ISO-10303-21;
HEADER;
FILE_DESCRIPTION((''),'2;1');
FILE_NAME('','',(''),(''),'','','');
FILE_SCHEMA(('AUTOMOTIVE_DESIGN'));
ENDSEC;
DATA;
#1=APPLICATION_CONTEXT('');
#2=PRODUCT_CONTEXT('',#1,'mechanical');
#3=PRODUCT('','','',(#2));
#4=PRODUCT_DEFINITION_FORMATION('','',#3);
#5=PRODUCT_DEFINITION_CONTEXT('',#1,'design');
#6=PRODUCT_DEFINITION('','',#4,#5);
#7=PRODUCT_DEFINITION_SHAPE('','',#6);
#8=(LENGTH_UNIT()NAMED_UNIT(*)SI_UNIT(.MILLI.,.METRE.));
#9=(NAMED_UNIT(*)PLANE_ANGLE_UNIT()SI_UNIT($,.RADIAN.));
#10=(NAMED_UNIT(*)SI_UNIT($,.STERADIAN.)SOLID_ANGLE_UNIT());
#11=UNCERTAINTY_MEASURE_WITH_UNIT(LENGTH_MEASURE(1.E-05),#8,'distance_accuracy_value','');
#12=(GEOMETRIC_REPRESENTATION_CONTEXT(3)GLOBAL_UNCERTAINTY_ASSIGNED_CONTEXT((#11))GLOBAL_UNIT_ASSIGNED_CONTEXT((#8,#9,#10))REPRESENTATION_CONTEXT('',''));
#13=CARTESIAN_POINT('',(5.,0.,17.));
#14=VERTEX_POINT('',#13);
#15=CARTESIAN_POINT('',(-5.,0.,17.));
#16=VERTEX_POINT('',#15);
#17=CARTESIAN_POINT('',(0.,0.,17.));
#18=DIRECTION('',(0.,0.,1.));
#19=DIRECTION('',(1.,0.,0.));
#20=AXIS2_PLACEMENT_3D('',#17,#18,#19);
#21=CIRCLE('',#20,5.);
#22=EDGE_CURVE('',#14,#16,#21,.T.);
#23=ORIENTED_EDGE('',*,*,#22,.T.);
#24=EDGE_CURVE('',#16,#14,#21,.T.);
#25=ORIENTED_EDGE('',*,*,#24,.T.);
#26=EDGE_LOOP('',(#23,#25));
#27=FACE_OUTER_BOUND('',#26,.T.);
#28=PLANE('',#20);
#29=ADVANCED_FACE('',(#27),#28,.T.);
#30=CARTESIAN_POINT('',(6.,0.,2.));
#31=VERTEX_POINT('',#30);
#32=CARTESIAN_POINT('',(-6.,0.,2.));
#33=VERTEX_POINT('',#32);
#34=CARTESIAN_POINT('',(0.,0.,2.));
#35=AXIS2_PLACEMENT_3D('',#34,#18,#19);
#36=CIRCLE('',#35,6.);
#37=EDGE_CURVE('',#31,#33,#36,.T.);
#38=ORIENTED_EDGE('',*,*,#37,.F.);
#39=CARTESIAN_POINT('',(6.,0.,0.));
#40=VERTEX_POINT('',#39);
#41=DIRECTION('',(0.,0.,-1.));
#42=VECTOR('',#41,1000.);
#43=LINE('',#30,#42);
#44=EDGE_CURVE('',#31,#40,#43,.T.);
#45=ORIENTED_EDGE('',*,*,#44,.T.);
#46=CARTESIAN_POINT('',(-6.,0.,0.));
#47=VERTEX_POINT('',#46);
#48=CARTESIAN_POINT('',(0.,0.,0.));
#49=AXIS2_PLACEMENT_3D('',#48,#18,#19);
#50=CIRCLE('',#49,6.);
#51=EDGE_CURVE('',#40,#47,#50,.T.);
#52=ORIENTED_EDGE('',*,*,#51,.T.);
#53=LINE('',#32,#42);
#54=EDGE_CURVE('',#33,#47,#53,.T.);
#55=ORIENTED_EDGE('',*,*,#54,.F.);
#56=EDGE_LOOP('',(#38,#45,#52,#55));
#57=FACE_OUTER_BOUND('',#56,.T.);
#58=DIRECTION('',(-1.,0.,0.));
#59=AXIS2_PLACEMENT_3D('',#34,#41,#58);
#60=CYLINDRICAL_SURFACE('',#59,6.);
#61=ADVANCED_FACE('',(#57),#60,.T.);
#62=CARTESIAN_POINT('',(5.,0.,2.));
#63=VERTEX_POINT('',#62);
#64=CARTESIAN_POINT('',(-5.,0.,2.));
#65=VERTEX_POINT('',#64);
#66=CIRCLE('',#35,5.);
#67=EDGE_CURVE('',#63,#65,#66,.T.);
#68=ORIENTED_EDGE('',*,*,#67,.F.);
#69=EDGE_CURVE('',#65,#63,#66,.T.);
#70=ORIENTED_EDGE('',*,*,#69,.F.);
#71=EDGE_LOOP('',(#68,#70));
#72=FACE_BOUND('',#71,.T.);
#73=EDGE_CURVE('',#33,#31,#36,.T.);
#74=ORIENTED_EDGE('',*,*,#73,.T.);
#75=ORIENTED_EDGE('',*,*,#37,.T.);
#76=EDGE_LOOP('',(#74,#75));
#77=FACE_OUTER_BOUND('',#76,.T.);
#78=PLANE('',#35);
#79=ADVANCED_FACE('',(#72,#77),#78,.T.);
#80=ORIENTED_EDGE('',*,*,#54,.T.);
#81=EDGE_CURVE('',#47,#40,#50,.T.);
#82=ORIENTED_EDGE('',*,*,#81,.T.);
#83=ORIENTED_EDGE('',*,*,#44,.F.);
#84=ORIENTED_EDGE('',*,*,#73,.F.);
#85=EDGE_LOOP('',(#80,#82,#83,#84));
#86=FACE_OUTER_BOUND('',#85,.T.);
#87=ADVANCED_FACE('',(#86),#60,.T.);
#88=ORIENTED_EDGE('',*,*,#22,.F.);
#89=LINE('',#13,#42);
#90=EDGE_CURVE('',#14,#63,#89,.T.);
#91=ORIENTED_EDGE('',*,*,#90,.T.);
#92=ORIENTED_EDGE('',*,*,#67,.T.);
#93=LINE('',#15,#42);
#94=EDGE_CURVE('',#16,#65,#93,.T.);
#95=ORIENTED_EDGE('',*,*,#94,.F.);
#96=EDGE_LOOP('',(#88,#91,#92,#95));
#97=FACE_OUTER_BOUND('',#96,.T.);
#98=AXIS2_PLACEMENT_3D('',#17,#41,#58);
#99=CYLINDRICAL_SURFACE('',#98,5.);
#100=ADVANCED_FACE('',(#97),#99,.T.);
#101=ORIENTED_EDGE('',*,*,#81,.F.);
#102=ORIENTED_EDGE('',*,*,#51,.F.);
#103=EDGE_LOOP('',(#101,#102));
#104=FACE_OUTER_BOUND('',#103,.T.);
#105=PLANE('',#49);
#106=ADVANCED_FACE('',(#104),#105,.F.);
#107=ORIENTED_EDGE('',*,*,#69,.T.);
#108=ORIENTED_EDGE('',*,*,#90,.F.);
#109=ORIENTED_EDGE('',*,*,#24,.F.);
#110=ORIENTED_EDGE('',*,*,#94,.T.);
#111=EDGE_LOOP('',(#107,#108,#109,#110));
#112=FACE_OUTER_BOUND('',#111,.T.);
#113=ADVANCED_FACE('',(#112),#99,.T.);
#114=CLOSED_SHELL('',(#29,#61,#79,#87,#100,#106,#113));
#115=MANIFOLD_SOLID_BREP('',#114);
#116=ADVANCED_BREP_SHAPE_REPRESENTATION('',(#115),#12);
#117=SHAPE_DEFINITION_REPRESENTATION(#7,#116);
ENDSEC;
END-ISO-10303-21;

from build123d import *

# Parameters (mm, degrees)
SKETCH1_R           = 6
BOSS_EXTRUDE1_DEPTH = 2
SKETCH2_R           = 5
BOSS_EXTRUDE2_DEPTH = 15


with BuildPart() as part:
    # Sketch1 → Boss-Extrude1 (new body)
    with BuildSketch(Plane.XY):
        Circle(SKETCH1_R)
    extrude(amount=BOSS_EXTRUDE1_DEPTH)

    # Sketch2 → Boss-Extrude2 (add)
    with BuildSketch(Plane.XY.offset(2)):
        Circle(SKETCH2_R)
    extrude(amount=BOSS_EXTRUDE2_DEPTH)


solid = part.part
